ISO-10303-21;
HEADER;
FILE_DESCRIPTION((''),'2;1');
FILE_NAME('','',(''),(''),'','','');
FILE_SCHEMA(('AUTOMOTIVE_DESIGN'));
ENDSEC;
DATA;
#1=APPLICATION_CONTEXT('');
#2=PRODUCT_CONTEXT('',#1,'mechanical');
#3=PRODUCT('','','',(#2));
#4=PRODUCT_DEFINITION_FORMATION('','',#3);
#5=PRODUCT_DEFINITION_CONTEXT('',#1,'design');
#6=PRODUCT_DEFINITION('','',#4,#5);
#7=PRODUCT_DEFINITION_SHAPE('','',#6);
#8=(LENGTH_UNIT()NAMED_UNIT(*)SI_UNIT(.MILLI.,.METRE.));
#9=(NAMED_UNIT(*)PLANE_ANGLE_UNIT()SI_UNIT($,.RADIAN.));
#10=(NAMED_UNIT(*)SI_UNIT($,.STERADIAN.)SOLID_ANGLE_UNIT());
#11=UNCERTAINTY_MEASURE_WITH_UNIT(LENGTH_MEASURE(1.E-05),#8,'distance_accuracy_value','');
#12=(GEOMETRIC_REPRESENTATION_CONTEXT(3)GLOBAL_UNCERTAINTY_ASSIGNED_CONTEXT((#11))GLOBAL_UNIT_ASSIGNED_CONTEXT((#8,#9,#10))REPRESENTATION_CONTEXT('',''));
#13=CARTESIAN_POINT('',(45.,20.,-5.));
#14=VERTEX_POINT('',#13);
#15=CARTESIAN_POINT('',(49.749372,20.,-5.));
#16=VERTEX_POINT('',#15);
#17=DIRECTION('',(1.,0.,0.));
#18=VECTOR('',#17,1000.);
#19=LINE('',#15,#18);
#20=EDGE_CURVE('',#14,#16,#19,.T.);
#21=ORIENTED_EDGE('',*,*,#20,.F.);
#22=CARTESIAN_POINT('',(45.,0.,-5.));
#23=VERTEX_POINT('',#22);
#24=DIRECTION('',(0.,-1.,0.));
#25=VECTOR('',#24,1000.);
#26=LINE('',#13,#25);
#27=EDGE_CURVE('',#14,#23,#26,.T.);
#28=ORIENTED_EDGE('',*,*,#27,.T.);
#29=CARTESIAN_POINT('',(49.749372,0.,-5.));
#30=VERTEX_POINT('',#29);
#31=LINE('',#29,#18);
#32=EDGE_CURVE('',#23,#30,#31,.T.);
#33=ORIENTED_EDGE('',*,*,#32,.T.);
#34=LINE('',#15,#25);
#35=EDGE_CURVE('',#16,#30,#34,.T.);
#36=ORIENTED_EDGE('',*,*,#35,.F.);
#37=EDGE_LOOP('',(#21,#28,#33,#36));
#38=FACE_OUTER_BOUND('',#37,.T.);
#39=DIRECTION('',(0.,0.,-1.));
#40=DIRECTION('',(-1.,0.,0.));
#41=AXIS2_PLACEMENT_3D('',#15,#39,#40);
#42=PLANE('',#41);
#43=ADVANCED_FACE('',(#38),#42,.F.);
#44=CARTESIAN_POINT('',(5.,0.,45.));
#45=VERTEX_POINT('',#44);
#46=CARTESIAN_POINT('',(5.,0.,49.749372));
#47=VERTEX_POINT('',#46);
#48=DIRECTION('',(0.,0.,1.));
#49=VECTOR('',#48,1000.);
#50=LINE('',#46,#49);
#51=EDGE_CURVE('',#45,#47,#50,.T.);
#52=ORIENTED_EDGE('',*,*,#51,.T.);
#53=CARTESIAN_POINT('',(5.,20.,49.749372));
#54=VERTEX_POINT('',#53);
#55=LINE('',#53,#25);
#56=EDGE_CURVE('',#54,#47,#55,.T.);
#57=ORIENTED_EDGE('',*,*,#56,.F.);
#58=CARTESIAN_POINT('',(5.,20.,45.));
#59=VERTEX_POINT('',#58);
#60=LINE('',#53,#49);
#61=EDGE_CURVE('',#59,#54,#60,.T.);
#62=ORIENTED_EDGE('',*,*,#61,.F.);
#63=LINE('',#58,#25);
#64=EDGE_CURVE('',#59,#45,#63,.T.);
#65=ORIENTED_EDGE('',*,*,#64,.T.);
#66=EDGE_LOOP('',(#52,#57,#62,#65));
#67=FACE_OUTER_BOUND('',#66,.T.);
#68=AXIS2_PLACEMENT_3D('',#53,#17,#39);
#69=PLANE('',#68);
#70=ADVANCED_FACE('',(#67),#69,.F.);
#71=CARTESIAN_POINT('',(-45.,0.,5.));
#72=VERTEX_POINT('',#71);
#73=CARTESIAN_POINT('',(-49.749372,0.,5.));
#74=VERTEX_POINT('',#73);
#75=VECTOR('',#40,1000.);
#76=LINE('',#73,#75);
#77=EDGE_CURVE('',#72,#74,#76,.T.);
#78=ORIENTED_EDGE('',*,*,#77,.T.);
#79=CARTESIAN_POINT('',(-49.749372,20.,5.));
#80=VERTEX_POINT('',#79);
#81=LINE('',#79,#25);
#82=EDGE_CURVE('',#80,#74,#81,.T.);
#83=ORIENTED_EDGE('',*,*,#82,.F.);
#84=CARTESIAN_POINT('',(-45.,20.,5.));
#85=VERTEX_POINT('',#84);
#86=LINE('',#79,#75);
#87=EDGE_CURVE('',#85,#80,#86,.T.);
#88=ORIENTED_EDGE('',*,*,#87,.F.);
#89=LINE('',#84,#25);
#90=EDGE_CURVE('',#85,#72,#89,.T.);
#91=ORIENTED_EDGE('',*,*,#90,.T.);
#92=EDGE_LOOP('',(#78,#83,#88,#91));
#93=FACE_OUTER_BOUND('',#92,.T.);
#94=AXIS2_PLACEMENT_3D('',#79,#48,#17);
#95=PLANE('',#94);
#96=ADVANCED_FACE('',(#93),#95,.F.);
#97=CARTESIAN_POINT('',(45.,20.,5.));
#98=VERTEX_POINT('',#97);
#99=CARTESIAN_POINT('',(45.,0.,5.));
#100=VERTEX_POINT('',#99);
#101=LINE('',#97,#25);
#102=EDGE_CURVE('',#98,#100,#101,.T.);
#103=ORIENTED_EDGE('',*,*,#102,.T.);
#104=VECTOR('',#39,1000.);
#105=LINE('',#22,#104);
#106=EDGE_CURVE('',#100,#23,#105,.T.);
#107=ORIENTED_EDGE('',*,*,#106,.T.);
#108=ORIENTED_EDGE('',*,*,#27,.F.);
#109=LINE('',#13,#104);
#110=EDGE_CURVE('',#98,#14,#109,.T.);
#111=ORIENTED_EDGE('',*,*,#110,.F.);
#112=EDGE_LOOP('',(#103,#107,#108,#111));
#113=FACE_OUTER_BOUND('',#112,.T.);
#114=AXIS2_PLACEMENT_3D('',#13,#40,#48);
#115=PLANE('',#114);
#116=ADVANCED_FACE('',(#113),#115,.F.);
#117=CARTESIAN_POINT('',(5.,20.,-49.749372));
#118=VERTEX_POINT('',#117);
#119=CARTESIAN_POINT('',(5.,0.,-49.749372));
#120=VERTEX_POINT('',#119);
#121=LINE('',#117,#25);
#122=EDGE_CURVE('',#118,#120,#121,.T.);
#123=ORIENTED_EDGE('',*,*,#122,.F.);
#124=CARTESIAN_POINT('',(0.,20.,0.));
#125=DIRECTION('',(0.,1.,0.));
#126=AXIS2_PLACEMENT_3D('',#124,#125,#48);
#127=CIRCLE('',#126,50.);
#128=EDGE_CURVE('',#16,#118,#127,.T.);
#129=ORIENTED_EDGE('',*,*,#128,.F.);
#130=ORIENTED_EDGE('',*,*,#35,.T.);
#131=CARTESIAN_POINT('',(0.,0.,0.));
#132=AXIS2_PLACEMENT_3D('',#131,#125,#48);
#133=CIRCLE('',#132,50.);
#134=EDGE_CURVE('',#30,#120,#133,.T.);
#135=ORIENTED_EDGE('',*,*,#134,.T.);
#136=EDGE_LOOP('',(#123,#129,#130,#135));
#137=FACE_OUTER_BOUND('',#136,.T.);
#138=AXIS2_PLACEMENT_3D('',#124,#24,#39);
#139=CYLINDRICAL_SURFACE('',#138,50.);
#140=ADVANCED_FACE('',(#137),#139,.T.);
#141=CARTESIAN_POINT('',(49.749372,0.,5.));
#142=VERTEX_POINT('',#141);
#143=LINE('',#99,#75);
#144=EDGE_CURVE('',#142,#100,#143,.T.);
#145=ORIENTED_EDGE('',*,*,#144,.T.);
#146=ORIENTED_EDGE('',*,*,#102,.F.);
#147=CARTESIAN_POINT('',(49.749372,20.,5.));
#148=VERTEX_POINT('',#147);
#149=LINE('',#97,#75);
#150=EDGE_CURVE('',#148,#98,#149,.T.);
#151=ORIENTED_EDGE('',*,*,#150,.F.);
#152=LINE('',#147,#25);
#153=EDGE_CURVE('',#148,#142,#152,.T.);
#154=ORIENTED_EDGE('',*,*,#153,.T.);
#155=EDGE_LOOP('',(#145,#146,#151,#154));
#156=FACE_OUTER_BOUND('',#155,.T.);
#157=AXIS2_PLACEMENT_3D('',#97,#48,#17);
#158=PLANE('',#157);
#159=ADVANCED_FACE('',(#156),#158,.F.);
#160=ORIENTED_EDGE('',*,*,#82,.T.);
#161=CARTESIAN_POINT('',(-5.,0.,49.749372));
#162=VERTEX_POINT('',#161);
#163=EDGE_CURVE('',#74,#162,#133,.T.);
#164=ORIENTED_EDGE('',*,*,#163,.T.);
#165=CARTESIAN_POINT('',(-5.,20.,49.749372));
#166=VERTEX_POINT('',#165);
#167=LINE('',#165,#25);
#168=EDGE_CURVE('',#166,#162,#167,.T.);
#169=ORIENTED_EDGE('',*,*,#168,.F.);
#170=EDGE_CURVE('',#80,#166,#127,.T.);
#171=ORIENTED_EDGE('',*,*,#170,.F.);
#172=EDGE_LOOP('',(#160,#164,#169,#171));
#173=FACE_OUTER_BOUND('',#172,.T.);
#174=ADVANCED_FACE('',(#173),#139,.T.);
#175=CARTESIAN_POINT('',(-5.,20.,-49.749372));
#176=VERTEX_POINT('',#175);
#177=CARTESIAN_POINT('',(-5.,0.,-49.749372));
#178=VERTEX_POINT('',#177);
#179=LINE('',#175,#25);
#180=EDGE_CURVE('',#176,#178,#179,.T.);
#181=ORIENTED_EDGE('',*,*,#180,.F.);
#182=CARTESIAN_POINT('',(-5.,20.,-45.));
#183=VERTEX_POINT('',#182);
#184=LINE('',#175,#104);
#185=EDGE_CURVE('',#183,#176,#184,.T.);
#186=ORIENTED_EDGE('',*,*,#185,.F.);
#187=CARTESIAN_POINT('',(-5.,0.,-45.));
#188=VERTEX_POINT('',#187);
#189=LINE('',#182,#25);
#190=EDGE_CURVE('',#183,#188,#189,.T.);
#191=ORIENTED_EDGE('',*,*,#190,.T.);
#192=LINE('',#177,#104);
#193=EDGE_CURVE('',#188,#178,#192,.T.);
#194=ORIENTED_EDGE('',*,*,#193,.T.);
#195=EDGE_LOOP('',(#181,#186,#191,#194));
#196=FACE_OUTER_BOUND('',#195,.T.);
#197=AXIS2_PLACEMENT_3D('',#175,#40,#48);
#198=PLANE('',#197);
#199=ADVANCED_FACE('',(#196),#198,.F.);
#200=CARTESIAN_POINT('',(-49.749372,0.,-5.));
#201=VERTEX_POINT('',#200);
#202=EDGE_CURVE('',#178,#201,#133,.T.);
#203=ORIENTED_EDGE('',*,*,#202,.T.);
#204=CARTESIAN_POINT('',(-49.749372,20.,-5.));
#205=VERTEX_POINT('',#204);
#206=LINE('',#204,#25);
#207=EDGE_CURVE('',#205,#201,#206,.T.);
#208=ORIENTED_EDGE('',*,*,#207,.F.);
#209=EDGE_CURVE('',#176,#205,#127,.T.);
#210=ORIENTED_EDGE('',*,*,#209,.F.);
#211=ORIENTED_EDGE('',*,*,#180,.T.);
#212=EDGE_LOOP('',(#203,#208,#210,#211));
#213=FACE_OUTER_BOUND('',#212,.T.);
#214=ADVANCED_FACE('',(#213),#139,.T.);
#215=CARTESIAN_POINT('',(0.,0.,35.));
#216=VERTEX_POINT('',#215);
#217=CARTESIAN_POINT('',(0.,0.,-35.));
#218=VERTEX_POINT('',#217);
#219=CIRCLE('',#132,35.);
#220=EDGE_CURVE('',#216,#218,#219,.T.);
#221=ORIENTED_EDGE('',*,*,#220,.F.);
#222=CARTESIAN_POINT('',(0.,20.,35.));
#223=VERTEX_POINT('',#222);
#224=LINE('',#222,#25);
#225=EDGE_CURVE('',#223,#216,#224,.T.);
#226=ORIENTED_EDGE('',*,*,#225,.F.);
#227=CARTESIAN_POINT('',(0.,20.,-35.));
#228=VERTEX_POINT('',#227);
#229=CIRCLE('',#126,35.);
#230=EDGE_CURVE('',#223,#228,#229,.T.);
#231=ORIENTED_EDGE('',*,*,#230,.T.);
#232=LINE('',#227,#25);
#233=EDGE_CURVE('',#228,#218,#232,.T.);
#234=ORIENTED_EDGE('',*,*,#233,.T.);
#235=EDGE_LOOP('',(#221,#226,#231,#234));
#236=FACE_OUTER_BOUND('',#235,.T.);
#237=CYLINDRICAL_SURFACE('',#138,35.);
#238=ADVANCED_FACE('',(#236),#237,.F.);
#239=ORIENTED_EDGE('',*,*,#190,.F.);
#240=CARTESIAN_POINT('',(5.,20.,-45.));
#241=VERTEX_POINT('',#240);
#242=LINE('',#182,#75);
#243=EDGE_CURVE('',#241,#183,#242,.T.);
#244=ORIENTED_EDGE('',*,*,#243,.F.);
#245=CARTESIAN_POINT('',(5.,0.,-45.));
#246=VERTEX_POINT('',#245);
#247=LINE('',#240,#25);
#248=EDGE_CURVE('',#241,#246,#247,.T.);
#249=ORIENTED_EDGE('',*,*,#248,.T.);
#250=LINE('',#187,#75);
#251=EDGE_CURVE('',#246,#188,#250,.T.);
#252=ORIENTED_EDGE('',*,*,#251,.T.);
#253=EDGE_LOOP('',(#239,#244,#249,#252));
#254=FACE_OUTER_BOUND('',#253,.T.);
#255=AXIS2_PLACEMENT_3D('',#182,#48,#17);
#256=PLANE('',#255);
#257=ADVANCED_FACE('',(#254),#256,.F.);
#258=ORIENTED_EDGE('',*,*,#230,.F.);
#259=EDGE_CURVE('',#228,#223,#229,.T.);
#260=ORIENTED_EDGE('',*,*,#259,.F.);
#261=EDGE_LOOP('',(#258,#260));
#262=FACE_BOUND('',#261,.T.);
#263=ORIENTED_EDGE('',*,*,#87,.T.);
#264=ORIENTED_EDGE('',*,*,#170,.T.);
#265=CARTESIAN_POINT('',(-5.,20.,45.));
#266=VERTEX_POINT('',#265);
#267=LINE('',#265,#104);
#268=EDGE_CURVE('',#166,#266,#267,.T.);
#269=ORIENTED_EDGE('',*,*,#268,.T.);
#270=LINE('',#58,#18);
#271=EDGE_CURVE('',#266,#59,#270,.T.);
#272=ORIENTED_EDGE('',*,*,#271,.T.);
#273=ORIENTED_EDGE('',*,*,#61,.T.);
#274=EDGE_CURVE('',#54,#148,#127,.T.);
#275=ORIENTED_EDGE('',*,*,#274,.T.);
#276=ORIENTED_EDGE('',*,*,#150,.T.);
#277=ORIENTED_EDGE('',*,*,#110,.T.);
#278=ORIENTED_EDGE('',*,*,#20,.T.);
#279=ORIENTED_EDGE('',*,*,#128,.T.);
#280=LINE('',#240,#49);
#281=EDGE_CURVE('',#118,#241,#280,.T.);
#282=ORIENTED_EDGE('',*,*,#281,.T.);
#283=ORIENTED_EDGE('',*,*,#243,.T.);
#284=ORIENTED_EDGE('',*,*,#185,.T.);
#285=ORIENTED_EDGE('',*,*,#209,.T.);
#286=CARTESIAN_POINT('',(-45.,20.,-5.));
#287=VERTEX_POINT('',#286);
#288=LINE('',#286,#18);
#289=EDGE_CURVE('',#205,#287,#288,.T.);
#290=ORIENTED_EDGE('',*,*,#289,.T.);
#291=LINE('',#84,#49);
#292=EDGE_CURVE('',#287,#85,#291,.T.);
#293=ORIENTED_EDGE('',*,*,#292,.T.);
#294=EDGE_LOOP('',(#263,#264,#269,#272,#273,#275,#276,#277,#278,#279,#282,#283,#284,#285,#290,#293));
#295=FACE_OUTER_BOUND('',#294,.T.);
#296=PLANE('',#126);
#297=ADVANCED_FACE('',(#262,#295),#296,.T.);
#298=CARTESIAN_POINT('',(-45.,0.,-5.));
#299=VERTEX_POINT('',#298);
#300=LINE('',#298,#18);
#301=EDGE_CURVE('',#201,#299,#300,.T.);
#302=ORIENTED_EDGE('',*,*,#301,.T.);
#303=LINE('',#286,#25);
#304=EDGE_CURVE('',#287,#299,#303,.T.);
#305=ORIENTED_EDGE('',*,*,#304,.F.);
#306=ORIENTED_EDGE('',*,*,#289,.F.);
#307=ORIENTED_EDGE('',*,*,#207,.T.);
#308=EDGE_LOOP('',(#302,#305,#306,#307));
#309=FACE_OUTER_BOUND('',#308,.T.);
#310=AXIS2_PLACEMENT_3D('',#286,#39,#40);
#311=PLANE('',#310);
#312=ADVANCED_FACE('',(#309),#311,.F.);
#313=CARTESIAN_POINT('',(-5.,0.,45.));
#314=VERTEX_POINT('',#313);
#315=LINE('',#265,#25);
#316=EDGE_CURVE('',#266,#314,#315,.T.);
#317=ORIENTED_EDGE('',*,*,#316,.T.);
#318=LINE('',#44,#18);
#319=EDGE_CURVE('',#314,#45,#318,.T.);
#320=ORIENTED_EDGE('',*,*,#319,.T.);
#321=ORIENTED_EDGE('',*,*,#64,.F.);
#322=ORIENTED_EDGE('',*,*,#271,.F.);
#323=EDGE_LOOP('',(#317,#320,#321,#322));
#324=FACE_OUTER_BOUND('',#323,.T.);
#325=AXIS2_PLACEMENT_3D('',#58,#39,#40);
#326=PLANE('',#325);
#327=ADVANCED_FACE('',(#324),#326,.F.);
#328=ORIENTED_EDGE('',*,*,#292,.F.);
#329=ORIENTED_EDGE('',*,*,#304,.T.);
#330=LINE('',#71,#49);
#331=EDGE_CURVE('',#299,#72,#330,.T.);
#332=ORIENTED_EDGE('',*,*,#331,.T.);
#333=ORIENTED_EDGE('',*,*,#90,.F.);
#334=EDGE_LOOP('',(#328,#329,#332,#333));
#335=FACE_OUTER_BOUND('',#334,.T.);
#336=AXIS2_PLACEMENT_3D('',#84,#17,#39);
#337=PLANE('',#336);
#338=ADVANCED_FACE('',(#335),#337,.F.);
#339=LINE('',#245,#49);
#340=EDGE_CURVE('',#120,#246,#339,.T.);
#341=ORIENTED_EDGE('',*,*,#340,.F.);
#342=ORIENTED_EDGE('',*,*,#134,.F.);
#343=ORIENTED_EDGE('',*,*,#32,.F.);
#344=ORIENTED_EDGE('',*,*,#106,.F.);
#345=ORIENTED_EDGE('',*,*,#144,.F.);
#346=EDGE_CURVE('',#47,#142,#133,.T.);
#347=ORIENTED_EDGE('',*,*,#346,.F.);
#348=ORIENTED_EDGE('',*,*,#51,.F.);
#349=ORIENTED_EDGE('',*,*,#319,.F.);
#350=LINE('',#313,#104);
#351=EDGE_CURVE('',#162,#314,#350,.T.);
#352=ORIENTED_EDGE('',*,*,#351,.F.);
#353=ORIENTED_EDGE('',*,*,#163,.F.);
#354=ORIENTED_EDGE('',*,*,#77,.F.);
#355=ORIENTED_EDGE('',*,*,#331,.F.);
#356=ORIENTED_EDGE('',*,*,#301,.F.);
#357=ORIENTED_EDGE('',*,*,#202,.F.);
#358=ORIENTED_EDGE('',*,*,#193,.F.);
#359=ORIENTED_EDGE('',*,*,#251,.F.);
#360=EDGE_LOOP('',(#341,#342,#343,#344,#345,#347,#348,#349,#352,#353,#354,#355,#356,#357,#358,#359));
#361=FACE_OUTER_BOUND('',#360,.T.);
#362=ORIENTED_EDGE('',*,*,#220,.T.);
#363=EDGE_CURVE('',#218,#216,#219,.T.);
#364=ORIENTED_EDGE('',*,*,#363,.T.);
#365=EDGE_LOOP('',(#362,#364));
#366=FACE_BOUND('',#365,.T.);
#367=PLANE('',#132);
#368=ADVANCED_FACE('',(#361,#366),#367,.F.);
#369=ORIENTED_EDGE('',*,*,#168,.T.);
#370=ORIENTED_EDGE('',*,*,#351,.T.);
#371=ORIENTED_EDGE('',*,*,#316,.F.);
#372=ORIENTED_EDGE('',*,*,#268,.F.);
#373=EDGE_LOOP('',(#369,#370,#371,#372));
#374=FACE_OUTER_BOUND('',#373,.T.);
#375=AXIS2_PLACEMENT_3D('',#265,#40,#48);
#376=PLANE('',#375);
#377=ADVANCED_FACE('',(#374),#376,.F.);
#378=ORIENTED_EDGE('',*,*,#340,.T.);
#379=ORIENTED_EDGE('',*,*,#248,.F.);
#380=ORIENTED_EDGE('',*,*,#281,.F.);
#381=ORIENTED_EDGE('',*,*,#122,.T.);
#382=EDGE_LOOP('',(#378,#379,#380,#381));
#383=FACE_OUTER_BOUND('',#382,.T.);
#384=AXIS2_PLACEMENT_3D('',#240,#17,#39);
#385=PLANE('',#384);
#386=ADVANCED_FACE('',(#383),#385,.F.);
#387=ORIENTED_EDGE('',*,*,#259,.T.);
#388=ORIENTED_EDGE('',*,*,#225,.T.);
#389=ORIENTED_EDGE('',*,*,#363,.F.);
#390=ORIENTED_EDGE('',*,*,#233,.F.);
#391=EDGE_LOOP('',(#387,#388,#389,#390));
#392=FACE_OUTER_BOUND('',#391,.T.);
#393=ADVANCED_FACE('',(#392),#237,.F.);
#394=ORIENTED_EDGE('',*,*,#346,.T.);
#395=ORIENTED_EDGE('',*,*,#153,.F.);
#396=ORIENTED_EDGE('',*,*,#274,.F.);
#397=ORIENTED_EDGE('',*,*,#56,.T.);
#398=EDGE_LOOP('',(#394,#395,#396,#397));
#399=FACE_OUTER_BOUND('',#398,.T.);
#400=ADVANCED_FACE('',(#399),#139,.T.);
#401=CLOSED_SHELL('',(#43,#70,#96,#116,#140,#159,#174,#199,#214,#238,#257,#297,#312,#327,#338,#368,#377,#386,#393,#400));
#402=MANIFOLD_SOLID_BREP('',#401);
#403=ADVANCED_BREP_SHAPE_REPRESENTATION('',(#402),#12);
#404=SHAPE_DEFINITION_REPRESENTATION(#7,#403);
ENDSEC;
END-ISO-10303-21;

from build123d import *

# Parameters (mm, degrees)
SKETCH1_R           = 35
BOSS_EXTRUDE1_DEPTH = 20


with BuildPart() as part:
    # Sketch1 → Boss-Extrude1 (new body)
    with BuildSketch(Plane(origin=(0, 0, 0), x_dir=(1, 0, 0), z_dir=(0, 1, 0))):
        with BuildLine():
            Line((-5, 49.749371855), (-5, 45))
            Line((-5, 45), (5, 45))
            Line((5, 45), (5, 49.749371855))
            ThreePointArc((5, 49.749371855), (35.355339059, 35.355339059), (49.749371855, 5))
            Line((49.749371855, 5), (45, 5))
            Line((45, 5), (45, -5))
            Line((45, -5), (49.749371855, -5))
            ThreePointArc((49.749371855, -5), (35.355339059, -35.355339059), (5, -49.749371855))
            Line((5, -49.749371855), (5, -45))
            Line((5, -45), (-5, -45))
            Line((-5, -45), (-5, -49.749371855))
            ThreePointArc((-5, -49.749371855), (-35.355339059, -35.355339059), (-49.749371855, -5))
            Line((-49.749371855, -5), (-45, -5))
            Line((-45, -5), (-45, 5))
            Line((-45, 5), (-49.749371855, 5))
            ThreePointArc((-49.749371855, 5), (-35.355339059, 35.355339059), (-5, 49.749371855))
        make_face()
        with Locations(Location((0, 0, 0), (0, 0, 270))):
            Circle(SKETCH1_R, mode=Mode.SUBTRACT)
    extrude(amount=BOSS_EXTRUDE1_DEPTH)


solid = part.part
